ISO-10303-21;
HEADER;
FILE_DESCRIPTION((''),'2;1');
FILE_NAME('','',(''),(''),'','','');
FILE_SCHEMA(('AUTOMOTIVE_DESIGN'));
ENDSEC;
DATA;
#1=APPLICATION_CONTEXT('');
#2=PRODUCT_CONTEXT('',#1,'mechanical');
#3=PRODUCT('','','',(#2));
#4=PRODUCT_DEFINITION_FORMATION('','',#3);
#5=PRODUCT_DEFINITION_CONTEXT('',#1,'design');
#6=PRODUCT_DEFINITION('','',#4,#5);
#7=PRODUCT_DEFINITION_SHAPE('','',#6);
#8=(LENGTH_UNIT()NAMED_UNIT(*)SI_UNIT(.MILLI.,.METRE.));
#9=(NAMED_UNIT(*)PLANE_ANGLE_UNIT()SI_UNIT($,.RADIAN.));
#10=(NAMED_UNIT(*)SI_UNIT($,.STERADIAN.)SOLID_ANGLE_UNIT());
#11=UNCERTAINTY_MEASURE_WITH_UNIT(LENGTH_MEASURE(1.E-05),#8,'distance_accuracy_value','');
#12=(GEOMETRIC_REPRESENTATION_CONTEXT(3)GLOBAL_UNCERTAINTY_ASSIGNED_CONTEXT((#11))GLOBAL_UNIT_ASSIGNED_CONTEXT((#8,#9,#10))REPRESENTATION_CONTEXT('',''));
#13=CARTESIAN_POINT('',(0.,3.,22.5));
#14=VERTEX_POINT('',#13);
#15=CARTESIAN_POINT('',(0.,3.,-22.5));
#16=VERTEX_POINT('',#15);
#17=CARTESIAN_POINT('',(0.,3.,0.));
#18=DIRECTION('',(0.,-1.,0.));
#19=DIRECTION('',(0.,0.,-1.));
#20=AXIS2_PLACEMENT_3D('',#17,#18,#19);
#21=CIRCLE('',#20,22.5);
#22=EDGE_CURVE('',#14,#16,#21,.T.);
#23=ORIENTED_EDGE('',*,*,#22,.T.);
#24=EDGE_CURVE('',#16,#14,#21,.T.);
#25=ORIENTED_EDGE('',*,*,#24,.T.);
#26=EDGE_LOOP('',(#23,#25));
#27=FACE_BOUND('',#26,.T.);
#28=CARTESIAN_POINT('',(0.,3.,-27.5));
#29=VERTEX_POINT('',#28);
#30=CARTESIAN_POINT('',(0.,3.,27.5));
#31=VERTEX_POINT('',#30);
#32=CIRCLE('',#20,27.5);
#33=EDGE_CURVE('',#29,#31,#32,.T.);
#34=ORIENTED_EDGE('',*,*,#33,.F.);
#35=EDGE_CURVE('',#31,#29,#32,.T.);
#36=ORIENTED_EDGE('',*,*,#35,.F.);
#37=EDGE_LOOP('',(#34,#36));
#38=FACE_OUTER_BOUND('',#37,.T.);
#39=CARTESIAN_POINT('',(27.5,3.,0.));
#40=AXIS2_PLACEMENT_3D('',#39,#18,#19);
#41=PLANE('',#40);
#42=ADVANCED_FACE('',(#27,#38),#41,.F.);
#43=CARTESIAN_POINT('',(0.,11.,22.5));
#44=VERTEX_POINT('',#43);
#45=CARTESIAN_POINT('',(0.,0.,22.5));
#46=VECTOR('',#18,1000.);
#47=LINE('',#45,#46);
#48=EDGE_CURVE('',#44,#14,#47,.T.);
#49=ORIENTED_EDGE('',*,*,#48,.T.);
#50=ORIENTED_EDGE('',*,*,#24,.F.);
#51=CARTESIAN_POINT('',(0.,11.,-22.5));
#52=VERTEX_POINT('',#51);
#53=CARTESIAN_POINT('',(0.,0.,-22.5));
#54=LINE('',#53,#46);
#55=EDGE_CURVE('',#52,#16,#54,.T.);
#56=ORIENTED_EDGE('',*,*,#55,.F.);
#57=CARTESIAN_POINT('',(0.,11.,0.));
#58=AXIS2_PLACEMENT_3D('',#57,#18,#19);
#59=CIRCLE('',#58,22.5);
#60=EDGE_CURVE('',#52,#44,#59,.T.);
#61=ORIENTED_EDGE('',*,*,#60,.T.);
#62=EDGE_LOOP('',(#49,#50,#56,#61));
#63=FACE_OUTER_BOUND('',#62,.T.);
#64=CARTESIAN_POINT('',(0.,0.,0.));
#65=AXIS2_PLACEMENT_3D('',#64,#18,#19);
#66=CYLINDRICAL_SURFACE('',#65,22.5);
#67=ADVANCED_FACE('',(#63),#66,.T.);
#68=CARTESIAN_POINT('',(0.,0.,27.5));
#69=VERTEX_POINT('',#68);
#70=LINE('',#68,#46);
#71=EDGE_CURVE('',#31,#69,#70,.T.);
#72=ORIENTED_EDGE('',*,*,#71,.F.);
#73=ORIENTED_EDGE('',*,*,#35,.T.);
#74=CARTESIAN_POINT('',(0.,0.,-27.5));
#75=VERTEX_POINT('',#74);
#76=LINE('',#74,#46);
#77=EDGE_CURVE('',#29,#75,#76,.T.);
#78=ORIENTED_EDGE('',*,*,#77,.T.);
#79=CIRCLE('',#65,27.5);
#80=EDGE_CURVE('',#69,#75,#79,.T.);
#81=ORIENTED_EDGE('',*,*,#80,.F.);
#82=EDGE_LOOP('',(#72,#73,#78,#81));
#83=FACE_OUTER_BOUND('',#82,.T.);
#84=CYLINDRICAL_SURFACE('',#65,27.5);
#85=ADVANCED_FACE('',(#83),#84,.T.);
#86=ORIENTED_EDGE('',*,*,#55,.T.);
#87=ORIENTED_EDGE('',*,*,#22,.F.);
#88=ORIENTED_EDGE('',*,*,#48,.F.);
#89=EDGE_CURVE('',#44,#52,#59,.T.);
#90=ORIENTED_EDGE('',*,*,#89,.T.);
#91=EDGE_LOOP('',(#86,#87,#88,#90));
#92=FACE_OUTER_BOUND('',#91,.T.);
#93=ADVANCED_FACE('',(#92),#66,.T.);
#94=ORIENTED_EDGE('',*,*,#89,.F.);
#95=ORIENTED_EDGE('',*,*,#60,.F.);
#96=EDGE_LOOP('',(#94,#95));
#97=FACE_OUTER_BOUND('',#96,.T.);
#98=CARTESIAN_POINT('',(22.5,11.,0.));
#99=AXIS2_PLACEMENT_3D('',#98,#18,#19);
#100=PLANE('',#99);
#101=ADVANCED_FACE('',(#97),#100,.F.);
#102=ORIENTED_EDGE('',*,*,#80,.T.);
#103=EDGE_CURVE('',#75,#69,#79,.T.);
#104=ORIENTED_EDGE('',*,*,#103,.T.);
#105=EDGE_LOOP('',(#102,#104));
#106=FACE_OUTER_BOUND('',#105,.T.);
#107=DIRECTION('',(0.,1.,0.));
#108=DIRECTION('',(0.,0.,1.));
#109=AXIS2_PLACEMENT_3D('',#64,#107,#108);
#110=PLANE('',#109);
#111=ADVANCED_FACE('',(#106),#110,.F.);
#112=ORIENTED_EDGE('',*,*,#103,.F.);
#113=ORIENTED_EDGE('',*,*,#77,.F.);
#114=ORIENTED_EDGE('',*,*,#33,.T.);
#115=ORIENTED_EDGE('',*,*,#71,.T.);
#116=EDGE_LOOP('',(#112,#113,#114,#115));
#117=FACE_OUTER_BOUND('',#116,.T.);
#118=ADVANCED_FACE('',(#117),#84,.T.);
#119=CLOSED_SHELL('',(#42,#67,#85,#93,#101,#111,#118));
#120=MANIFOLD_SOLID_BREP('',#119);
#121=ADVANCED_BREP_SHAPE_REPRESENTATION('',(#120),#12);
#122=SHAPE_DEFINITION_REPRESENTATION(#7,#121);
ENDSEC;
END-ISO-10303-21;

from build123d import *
from build123d.topology import SkipClean

# Parameters (mm, degrees)
REVOLVE_1_ANGLE           = 180
REVOLVE_1_OTHER_WAY_ANGLE = 180


with BuildPart() as part:
    # 草图1 → 旋转1 (revolve)
    with BuildSketch(Plane.XY):
        Polygon((0, 0), (-27.5, 0), (-27.5, 3), (-22.5, 3), (-22.5, 11), (0, 11), align=None)
    revolve(axis=Axis((0, 0, 0), (0, 1, 0)), revolution_arc=REVOLVE_1_ANGLE)

    # 草图1 → 旋转1 other way (revolve)
    with SkipClean():  # the faces are left unmerged after this step: merging them gives an invalid solid
        with BuildSketch(Plane.XY):
            Polygon((0, 0), (-27.5, 0), (-27.5, 3), (-22.5, 3), (-22.5, 11), (0, 11), align=None)
        revolve(axis=Axis((0, 0, 0), (0, -1, 0)), revolution_arc=REVOLVE_1_OTHER_WAY_ANGLE)


solid = part.part
